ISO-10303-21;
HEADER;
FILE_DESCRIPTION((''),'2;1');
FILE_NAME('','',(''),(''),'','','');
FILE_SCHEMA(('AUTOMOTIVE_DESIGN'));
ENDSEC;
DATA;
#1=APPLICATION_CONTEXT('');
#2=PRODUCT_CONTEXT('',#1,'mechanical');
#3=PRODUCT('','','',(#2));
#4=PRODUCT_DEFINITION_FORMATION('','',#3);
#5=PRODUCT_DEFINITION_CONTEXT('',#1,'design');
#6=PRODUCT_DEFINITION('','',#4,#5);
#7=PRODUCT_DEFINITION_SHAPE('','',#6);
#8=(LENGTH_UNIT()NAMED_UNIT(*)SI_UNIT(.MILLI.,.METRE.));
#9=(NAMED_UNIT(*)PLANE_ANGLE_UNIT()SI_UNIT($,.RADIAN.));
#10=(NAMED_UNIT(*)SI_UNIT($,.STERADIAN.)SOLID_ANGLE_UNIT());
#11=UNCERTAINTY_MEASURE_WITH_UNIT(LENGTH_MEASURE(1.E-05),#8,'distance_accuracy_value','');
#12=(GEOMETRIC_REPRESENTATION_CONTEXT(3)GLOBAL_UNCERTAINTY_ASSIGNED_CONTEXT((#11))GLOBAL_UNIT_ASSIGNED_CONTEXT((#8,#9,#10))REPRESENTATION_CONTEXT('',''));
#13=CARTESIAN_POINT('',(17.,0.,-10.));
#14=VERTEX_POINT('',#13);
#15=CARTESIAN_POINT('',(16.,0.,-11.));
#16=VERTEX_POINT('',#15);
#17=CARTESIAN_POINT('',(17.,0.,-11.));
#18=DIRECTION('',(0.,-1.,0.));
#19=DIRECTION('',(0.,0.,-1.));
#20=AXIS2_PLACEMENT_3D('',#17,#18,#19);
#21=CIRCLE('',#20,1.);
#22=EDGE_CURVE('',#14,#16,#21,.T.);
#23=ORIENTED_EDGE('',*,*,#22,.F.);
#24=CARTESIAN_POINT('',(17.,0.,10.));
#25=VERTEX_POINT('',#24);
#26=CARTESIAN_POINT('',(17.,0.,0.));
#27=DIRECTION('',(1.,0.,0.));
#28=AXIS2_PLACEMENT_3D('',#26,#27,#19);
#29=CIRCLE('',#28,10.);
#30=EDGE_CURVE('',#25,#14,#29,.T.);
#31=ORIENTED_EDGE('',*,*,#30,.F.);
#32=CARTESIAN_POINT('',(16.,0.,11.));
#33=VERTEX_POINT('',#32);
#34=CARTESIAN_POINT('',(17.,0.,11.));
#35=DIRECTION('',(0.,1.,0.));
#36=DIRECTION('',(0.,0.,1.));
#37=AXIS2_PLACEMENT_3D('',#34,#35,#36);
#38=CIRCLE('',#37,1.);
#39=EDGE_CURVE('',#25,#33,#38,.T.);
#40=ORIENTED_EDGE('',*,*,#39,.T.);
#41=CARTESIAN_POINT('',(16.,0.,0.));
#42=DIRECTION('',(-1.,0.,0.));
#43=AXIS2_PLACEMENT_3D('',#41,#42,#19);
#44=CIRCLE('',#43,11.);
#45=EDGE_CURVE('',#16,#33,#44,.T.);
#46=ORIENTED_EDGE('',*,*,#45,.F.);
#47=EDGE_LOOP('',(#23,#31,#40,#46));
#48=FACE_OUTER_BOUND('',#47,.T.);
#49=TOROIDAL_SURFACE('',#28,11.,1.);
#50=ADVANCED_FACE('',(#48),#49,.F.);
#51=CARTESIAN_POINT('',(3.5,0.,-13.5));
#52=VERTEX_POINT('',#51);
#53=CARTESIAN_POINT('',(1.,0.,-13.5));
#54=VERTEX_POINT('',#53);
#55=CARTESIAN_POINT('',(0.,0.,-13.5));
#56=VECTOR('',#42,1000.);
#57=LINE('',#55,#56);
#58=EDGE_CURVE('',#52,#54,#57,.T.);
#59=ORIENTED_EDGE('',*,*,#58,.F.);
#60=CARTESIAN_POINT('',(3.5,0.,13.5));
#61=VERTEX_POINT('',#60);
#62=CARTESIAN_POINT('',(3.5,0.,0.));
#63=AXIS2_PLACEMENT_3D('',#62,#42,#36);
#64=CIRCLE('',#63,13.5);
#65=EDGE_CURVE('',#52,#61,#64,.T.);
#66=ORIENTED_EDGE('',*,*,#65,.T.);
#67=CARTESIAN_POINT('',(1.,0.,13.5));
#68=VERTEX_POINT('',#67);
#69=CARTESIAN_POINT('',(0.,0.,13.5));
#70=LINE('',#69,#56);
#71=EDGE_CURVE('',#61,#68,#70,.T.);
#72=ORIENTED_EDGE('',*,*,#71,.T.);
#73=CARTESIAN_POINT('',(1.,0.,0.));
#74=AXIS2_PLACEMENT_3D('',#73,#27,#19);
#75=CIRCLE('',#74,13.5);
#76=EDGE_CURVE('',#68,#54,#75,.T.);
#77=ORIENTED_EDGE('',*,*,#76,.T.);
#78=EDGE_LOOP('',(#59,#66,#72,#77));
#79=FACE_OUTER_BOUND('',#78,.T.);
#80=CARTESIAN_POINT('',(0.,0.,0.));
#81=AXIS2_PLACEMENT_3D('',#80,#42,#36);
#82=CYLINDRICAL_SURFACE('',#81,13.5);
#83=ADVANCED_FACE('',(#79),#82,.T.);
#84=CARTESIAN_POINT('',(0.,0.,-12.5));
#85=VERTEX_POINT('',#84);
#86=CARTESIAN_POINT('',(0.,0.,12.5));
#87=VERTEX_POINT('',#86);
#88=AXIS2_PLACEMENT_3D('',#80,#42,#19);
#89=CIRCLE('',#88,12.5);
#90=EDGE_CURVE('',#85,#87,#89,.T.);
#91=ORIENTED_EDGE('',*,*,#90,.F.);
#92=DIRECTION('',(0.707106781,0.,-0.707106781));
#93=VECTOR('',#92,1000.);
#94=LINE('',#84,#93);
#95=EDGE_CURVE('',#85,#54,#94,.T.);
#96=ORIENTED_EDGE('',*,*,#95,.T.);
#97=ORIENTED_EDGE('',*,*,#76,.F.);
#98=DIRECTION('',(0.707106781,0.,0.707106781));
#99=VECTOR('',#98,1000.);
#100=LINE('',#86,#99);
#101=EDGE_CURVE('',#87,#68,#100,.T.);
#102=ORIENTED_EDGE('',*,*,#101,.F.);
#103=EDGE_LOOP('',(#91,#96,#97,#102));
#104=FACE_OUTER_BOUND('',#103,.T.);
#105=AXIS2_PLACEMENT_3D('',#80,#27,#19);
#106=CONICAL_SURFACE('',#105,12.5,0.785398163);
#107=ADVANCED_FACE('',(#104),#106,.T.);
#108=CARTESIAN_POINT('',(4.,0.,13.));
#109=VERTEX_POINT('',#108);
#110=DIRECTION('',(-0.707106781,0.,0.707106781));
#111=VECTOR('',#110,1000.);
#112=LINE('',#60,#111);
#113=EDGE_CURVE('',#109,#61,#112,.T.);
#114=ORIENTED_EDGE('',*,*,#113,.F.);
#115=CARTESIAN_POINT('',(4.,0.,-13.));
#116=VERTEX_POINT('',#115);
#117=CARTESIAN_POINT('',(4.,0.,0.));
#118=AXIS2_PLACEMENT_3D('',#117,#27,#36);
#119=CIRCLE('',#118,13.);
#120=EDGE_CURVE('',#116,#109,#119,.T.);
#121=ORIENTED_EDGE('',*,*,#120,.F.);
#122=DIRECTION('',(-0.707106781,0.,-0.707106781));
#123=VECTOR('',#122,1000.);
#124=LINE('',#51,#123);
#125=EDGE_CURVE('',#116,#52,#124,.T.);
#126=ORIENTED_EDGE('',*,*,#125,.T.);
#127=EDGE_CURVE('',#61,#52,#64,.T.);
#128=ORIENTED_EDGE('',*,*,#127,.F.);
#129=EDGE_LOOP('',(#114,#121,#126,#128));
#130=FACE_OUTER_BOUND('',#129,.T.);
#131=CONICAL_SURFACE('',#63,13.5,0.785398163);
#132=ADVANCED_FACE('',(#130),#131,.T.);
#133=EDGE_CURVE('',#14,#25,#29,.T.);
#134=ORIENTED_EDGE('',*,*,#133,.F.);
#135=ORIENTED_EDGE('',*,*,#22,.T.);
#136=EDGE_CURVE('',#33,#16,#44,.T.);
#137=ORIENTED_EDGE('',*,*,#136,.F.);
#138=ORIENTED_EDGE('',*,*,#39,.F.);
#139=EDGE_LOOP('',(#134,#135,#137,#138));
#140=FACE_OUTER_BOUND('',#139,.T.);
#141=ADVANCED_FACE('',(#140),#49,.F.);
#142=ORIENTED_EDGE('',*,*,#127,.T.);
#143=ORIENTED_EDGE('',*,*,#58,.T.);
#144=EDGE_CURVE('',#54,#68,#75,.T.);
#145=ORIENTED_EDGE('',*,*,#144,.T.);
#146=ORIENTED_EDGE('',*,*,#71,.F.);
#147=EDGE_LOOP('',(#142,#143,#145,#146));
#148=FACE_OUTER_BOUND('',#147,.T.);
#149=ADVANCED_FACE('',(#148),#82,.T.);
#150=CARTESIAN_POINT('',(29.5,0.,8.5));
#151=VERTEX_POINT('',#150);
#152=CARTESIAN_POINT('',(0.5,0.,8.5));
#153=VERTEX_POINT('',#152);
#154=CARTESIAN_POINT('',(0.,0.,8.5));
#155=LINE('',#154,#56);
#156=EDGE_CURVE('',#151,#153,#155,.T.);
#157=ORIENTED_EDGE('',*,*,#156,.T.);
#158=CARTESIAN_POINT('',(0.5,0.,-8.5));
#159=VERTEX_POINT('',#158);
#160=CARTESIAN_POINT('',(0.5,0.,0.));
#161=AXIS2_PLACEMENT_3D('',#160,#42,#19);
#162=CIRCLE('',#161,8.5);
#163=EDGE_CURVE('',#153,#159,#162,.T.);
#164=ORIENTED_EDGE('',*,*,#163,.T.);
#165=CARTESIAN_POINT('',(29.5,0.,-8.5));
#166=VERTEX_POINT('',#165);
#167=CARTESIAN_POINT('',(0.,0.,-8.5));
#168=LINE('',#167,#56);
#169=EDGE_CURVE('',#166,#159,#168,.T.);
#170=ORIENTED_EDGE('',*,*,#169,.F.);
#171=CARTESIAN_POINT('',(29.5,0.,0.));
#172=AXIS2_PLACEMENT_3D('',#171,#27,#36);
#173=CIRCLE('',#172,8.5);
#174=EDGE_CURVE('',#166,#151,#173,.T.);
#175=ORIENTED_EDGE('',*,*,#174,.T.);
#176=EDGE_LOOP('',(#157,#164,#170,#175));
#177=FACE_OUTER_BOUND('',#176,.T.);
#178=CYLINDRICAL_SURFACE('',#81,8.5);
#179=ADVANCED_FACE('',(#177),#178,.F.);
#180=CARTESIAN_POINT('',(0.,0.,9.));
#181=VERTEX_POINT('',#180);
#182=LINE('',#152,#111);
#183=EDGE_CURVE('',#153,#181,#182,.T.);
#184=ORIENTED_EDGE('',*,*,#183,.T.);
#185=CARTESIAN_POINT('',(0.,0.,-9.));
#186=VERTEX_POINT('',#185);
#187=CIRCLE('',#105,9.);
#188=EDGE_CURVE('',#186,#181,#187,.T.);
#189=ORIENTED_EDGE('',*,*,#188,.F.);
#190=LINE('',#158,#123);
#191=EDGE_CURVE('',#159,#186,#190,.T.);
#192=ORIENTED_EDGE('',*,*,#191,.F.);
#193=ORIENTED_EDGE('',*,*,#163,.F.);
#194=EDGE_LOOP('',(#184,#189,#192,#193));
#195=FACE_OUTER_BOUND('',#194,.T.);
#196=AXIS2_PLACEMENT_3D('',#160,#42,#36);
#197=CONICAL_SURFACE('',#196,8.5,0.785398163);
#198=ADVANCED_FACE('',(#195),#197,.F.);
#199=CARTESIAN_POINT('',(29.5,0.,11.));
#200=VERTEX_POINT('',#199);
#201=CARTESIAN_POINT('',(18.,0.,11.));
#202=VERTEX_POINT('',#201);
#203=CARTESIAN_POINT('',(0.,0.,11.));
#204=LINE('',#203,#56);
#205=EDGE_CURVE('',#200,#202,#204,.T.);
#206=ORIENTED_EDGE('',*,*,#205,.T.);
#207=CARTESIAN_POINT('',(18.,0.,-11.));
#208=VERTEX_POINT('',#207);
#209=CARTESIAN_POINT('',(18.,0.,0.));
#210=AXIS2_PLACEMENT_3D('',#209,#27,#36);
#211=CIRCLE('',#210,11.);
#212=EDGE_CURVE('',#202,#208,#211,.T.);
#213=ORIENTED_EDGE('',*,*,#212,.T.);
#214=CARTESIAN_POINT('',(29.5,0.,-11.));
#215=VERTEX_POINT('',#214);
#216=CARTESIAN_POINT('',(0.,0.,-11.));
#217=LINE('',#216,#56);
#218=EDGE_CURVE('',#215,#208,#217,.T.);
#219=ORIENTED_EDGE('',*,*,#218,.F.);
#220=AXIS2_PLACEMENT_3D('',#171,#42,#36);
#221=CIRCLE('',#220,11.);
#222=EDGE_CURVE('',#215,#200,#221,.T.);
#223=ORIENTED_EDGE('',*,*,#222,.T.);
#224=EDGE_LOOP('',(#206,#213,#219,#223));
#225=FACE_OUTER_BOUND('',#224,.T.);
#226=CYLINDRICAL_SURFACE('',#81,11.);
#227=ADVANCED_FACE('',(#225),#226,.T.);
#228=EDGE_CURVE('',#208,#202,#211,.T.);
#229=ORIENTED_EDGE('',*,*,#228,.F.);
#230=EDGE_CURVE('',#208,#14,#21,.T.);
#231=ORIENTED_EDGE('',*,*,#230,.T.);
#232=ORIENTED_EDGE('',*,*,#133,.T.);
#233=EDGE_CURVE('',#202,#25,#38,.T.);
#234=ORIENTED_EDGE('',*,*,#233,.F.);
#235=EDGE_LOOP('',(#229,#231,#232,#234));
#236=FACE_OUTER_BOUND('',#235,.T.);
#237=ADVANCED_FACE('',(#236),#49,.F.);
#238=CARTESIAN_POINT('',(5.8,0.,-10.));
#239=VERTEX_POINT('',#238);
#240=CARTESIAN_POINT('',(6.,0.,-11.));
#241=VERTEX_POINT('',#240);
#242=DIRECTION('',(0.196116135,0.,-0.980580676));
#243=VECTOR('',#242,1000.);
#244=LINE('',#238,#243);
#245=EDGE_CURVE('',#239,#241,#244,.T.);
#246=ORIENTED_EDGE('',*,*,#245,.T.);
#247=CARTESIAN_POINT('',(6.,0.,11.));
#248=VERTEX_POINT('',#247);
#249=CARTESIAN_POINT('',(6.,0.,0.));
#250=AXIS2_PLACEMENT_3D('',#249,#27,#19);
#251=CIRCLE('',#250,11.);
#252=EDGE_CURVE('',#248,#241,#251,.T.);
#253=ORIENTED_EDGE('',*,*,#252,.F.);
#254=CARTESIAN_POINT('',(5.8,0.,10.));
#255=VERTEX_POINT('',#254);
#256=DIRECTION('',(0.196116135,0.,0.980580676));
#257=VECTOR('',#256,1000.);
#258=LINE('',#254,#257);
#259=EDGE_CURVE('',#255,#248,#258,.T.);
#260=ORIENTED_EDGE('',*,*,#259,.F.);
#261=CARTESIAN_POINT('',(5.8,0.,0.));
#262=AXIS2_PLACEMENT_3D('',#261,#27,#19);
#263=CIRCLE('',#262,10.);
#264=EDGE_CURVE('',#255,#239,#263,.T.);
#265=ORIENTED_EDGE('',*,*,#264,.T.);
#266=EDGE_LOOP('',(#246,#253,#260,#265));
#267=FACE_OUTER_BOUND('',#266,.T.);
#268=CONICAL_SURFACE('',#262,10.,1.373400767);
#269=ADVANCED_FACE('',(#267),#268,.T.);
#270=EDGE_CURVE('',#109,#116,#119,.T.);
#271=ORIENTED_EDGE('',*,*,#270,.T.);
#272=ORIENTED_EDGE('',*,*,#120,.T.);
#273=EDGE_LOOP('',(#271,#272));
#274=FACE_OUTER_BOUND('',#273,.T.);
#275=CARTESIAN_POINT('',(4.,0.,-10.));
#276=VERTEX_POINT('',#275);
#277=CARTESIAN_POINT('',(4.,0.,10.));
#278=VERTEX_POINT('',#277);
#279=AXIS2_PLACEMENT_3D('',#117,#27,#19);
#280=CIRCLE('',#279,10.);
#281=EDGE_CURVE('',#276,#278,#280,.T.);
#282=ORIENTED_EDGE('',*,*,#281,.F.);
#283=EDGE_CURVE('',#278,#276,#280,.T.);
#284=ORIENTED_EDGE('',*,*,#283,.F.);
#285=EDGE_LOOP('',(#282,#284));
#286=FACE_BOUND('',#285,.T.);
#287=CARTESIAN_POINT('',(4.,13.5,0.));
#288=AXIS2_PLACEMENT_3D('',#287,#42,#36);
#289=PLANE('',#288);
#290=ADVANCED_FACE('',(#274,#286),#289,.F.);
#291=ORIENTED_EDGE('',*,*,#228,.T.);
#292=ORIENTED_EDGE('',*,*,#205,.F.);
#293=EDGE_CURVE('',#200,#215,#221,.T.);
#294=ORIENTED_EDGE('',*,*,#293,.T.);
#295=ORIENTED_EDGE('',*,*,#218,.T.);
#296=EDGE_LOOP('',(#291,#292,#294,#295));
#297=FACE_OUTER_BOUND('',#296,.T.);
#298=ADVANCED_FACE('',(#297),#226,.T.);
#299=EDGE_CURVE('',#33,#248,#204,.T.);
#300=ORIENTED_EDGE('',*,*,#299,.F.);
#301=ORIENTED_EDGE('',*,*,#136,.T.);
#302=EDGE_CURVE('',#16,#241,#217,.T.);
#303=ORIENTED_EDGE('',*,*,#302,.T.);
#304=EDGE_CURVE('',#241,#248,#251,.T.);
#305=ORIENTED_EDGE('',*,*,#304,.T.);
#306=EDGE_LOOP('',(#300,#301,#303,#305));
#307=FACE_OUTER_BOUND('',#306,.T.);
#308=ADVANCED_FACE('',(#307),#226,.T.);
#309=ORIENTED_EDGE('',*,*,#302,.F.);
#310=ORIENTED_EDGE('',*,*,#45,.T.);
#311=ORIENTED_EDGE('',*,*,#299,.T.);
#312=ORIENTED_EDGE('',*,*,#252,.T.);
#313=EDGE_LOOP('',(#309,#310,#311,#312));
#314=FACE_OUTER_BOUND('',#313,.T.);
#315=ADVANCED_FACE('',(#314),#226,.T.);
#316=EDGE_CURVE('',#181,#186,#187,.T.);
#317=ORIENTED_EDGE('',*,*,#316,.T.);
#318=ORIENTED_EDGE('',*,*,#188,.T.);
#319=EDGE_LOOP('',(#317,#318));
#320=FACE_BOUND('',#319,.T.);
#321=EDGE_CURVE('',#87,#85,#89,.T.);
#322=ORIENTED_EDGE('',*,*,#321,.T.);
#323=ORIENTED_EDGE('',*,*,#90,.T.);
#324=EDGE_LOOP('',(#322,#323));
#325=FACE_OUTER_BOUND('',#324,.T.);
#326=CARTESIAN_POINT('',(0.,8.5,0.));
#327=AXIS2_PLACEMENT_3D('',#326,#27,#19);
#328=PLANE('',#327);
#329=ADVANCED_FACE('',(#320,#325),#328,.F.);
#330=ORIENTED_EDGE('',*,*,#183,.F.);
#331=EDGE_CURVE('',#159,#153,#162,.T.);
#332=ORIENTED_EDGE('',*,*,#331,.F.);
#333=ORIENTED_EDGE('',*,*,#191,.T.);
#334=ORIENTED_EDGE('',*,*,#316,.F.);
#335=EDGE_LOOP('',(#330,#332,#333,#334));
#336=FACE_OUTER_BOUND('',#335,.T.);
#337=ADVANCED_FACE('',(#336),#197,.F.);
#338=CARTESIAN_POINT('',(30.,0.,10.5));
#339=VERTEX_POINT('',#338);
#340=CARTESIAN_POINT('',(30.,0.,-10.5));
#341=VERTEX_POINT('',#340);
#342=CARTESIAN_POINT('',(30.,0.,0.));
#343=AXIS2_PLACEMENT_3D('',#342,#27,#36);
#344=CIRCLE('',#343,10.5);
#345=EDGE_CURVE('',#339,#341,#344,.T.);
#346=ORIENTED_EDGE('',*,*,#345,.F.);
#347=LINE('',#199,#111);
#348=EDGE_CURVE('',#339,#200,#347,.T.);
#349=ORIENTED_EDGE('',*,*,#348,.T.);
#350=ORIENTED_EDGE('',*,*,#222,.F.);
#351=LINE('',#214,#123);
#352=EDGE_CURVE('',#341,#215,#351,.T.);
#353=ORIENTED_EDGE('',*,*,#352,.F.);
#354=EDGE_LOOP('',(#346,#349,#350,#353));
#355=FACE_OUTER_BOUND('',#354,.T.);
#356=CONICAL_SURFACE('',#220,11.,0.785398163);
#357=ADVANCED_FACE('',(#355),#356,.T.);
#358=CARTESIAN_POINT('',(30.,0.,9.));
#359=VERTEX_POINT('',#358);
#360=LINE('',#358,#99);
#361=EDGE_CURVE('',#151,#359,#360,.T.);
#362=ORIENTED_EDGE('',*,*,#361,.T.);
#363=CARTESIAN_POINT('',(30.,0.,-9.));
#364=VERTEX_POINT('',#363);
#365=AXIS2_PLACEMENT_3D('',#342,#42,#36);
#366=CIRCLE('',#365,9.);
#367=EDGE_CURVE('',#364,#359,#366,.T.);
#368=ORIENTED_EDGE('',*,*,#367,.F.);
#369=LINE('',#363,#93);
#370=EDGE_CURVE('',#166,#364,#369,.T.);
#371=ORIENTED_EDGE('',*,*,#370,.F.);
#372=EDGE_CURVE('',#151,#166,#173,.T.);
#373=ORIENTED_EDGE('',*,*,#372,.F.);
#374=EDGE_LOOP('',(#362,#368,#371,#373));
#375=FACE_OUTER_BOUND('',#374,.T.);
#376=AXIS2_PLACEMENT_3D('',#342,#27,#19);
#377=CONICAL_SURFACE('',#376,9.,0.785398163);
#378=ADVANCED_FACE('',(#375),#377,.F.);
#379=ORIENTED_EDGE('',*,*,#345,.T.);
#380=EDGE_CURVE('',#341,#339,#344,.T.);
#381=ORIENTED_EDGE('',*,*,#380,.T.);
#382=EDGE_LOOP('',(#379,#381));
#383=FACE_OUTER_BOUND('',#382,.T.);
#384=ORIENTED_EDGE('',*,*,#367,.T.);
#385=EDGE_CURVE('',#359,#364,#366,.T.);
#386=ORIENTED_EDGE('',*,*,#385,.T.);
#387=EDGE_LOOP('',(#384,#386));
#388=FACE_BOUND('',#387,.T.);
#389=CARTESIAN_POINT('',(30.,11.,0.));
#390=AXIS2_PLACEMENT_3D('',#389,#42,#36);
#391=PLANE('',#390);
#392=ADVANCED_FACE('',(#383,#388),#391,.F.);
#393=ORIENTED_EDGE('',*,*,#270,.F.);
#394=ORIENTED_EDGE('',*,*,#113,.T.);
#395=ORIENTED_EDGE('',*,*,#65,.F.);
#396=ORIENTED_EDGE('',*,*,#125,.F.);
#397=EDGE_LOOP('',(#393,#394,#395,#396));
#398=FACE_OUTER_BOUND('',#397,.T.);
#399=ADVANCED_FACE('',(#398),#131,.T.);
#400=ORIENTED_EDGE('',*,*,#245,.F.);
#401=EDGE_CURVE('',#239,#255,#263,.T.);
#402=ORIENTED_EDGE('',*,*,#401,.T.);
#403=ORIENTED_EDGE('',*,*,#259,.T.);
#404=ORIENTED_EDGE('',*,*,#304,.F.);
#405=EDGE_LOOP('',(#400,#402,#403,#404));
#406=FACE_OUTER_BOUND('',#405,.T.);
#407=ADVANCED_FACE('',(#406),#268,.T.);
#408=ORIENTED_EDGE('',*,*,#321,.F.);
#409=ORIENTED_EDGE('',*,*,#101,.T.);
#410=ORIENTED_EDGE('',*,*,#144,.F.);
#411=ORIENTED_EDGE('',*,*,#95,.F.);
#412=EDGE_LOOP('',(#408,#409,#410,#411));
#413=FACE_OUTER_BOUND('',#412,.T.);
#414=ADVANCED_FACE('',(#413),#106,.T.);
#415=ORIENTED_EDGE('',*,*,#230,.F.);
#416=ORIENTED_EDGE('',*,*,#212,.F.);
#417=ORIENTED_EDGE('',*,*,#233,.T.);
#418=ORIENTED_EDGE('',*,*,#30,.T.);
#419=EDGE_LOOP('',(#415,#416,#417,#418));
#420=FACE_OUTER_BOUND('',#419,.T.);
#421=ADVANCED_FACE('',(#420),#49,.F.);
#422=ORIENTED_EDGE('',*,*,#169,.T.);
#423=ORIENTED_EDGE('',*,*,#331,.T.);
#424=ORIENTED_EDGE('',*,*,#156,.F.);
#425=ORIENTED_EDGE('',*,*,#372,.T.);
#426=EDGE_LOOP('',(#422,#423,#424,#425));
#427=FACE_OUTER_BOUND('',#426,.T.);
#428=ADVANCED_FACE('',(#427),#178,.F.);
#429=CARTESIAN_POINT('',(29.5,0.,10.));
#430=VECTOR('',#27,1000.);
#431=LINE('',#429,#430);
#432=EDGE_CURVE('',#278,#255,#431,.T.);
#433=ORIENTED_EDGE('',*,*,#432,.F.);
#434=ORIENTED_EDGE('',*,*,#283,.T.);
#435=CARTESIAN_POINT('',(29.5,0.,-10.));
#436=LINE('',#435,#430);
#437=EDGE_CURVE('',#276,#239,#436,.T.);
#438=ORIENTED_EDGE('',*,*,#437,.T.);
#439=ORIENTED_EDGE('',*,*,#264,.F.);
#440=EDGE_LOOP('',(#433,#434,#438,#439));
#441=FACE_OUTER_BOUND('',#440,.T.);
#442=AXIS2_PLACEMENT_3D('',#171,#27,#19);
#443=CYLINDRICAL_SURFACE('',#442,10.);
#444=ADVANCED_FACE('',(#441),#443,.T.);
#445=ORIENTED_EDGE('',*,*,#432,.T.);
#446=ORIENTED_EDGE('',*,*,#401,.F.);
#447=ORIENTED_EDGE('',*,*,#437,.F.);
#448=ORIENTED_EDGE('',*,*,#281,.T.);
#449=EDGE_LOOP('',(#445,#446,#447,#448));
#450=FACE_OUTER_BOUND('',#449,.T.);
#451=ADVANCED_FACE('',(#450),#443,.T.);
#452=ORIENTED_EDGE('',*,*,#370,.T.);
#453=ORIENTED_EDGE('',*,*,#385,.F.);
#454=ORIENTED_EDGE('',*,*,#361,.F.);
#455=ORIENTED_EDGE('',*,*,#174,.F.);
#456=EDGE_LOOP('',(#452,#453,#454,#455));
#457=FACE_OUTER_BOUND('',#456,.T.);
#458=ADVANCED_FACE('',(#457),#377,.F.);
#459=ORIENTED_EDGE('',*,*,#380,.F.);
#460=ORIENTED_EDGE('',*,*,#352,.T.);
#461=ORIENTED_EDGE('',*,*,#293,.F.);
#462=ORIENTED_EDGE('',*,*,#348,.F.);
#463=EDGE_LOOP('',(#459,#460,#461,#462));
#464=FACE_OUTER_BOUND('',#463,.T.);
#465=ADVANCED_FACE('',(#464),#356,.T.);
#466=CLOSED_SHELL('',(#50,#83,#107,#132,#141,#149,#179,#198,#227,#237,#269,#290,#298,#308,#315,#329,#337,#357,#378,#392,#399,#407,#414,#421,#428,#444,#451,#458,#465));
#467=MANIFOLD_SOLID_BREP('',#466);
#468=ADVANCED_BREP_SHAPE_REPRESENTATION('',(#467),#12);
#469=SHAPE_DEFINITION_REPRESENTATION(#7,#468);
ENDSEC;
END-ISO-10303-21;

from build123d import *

# Parameters (mm, degrees)
CHAMFER1_SIZE = 1
CHAMFER2_SIZE = 0.5
SKETCH2_R     = 1


with BuildPart() as part:
    # Sketch1 → Revolve1 (revolve)
    with BuildSketch(Plane.XY, mode=Mode.PRIVATE) as revolve1_sk:
        Polygon((30, 8.5), (0, 8.5), (0, 13.5), (4, 13.5), (4, 11), (30, 11), align=None)
    revolve(revolve1_sk.sketch.rotate(Axis((0, 0, 0), (1, 0, 0)), 90), axis=Axis((0, 0, 0), (1, 0, 0)))

    # Chamfer1
    chamfer1_edges = [part.edges().sort_by_distance(p)[0] for p in [
        (0, 0, -13.5),
    ]]
    chamfer(chamfer1_edges, length=CHAMFER1_SIZE)

    # Chamfer2
    chamfer2_edges = [part.edges().sort_by_distance(p)[0] for p in [
        (30, 0, -11),
        (4, 0, -13.5),
        (0, 0, -8.5),
        (30, 0, -8.5),
    ]]
    chamfer(chamfer2_edges, length=CHAMFER2_SIZE)

    # Sketch2 → Cut-Revolve1 (revolve, cut)
    with BuildSketch(Plane(origin=(0, 0, 0), x_dir=(1, 0, 0), z_dir=(0, 1, 0))):
        with Locations((32, 11)):
            Circle(SKETCH2_R)
        with Locations((17, 11)):
            Circle(SKETCH2_R)
        Polygon((4, 11), (4, 10), (5.8, 10), (6, 11), align=None)
    revolve(axis=Axis((29.5, 0, 0), (-1, 0, 0)), mode=Mode.SUBTRACT)


solid = part.part
